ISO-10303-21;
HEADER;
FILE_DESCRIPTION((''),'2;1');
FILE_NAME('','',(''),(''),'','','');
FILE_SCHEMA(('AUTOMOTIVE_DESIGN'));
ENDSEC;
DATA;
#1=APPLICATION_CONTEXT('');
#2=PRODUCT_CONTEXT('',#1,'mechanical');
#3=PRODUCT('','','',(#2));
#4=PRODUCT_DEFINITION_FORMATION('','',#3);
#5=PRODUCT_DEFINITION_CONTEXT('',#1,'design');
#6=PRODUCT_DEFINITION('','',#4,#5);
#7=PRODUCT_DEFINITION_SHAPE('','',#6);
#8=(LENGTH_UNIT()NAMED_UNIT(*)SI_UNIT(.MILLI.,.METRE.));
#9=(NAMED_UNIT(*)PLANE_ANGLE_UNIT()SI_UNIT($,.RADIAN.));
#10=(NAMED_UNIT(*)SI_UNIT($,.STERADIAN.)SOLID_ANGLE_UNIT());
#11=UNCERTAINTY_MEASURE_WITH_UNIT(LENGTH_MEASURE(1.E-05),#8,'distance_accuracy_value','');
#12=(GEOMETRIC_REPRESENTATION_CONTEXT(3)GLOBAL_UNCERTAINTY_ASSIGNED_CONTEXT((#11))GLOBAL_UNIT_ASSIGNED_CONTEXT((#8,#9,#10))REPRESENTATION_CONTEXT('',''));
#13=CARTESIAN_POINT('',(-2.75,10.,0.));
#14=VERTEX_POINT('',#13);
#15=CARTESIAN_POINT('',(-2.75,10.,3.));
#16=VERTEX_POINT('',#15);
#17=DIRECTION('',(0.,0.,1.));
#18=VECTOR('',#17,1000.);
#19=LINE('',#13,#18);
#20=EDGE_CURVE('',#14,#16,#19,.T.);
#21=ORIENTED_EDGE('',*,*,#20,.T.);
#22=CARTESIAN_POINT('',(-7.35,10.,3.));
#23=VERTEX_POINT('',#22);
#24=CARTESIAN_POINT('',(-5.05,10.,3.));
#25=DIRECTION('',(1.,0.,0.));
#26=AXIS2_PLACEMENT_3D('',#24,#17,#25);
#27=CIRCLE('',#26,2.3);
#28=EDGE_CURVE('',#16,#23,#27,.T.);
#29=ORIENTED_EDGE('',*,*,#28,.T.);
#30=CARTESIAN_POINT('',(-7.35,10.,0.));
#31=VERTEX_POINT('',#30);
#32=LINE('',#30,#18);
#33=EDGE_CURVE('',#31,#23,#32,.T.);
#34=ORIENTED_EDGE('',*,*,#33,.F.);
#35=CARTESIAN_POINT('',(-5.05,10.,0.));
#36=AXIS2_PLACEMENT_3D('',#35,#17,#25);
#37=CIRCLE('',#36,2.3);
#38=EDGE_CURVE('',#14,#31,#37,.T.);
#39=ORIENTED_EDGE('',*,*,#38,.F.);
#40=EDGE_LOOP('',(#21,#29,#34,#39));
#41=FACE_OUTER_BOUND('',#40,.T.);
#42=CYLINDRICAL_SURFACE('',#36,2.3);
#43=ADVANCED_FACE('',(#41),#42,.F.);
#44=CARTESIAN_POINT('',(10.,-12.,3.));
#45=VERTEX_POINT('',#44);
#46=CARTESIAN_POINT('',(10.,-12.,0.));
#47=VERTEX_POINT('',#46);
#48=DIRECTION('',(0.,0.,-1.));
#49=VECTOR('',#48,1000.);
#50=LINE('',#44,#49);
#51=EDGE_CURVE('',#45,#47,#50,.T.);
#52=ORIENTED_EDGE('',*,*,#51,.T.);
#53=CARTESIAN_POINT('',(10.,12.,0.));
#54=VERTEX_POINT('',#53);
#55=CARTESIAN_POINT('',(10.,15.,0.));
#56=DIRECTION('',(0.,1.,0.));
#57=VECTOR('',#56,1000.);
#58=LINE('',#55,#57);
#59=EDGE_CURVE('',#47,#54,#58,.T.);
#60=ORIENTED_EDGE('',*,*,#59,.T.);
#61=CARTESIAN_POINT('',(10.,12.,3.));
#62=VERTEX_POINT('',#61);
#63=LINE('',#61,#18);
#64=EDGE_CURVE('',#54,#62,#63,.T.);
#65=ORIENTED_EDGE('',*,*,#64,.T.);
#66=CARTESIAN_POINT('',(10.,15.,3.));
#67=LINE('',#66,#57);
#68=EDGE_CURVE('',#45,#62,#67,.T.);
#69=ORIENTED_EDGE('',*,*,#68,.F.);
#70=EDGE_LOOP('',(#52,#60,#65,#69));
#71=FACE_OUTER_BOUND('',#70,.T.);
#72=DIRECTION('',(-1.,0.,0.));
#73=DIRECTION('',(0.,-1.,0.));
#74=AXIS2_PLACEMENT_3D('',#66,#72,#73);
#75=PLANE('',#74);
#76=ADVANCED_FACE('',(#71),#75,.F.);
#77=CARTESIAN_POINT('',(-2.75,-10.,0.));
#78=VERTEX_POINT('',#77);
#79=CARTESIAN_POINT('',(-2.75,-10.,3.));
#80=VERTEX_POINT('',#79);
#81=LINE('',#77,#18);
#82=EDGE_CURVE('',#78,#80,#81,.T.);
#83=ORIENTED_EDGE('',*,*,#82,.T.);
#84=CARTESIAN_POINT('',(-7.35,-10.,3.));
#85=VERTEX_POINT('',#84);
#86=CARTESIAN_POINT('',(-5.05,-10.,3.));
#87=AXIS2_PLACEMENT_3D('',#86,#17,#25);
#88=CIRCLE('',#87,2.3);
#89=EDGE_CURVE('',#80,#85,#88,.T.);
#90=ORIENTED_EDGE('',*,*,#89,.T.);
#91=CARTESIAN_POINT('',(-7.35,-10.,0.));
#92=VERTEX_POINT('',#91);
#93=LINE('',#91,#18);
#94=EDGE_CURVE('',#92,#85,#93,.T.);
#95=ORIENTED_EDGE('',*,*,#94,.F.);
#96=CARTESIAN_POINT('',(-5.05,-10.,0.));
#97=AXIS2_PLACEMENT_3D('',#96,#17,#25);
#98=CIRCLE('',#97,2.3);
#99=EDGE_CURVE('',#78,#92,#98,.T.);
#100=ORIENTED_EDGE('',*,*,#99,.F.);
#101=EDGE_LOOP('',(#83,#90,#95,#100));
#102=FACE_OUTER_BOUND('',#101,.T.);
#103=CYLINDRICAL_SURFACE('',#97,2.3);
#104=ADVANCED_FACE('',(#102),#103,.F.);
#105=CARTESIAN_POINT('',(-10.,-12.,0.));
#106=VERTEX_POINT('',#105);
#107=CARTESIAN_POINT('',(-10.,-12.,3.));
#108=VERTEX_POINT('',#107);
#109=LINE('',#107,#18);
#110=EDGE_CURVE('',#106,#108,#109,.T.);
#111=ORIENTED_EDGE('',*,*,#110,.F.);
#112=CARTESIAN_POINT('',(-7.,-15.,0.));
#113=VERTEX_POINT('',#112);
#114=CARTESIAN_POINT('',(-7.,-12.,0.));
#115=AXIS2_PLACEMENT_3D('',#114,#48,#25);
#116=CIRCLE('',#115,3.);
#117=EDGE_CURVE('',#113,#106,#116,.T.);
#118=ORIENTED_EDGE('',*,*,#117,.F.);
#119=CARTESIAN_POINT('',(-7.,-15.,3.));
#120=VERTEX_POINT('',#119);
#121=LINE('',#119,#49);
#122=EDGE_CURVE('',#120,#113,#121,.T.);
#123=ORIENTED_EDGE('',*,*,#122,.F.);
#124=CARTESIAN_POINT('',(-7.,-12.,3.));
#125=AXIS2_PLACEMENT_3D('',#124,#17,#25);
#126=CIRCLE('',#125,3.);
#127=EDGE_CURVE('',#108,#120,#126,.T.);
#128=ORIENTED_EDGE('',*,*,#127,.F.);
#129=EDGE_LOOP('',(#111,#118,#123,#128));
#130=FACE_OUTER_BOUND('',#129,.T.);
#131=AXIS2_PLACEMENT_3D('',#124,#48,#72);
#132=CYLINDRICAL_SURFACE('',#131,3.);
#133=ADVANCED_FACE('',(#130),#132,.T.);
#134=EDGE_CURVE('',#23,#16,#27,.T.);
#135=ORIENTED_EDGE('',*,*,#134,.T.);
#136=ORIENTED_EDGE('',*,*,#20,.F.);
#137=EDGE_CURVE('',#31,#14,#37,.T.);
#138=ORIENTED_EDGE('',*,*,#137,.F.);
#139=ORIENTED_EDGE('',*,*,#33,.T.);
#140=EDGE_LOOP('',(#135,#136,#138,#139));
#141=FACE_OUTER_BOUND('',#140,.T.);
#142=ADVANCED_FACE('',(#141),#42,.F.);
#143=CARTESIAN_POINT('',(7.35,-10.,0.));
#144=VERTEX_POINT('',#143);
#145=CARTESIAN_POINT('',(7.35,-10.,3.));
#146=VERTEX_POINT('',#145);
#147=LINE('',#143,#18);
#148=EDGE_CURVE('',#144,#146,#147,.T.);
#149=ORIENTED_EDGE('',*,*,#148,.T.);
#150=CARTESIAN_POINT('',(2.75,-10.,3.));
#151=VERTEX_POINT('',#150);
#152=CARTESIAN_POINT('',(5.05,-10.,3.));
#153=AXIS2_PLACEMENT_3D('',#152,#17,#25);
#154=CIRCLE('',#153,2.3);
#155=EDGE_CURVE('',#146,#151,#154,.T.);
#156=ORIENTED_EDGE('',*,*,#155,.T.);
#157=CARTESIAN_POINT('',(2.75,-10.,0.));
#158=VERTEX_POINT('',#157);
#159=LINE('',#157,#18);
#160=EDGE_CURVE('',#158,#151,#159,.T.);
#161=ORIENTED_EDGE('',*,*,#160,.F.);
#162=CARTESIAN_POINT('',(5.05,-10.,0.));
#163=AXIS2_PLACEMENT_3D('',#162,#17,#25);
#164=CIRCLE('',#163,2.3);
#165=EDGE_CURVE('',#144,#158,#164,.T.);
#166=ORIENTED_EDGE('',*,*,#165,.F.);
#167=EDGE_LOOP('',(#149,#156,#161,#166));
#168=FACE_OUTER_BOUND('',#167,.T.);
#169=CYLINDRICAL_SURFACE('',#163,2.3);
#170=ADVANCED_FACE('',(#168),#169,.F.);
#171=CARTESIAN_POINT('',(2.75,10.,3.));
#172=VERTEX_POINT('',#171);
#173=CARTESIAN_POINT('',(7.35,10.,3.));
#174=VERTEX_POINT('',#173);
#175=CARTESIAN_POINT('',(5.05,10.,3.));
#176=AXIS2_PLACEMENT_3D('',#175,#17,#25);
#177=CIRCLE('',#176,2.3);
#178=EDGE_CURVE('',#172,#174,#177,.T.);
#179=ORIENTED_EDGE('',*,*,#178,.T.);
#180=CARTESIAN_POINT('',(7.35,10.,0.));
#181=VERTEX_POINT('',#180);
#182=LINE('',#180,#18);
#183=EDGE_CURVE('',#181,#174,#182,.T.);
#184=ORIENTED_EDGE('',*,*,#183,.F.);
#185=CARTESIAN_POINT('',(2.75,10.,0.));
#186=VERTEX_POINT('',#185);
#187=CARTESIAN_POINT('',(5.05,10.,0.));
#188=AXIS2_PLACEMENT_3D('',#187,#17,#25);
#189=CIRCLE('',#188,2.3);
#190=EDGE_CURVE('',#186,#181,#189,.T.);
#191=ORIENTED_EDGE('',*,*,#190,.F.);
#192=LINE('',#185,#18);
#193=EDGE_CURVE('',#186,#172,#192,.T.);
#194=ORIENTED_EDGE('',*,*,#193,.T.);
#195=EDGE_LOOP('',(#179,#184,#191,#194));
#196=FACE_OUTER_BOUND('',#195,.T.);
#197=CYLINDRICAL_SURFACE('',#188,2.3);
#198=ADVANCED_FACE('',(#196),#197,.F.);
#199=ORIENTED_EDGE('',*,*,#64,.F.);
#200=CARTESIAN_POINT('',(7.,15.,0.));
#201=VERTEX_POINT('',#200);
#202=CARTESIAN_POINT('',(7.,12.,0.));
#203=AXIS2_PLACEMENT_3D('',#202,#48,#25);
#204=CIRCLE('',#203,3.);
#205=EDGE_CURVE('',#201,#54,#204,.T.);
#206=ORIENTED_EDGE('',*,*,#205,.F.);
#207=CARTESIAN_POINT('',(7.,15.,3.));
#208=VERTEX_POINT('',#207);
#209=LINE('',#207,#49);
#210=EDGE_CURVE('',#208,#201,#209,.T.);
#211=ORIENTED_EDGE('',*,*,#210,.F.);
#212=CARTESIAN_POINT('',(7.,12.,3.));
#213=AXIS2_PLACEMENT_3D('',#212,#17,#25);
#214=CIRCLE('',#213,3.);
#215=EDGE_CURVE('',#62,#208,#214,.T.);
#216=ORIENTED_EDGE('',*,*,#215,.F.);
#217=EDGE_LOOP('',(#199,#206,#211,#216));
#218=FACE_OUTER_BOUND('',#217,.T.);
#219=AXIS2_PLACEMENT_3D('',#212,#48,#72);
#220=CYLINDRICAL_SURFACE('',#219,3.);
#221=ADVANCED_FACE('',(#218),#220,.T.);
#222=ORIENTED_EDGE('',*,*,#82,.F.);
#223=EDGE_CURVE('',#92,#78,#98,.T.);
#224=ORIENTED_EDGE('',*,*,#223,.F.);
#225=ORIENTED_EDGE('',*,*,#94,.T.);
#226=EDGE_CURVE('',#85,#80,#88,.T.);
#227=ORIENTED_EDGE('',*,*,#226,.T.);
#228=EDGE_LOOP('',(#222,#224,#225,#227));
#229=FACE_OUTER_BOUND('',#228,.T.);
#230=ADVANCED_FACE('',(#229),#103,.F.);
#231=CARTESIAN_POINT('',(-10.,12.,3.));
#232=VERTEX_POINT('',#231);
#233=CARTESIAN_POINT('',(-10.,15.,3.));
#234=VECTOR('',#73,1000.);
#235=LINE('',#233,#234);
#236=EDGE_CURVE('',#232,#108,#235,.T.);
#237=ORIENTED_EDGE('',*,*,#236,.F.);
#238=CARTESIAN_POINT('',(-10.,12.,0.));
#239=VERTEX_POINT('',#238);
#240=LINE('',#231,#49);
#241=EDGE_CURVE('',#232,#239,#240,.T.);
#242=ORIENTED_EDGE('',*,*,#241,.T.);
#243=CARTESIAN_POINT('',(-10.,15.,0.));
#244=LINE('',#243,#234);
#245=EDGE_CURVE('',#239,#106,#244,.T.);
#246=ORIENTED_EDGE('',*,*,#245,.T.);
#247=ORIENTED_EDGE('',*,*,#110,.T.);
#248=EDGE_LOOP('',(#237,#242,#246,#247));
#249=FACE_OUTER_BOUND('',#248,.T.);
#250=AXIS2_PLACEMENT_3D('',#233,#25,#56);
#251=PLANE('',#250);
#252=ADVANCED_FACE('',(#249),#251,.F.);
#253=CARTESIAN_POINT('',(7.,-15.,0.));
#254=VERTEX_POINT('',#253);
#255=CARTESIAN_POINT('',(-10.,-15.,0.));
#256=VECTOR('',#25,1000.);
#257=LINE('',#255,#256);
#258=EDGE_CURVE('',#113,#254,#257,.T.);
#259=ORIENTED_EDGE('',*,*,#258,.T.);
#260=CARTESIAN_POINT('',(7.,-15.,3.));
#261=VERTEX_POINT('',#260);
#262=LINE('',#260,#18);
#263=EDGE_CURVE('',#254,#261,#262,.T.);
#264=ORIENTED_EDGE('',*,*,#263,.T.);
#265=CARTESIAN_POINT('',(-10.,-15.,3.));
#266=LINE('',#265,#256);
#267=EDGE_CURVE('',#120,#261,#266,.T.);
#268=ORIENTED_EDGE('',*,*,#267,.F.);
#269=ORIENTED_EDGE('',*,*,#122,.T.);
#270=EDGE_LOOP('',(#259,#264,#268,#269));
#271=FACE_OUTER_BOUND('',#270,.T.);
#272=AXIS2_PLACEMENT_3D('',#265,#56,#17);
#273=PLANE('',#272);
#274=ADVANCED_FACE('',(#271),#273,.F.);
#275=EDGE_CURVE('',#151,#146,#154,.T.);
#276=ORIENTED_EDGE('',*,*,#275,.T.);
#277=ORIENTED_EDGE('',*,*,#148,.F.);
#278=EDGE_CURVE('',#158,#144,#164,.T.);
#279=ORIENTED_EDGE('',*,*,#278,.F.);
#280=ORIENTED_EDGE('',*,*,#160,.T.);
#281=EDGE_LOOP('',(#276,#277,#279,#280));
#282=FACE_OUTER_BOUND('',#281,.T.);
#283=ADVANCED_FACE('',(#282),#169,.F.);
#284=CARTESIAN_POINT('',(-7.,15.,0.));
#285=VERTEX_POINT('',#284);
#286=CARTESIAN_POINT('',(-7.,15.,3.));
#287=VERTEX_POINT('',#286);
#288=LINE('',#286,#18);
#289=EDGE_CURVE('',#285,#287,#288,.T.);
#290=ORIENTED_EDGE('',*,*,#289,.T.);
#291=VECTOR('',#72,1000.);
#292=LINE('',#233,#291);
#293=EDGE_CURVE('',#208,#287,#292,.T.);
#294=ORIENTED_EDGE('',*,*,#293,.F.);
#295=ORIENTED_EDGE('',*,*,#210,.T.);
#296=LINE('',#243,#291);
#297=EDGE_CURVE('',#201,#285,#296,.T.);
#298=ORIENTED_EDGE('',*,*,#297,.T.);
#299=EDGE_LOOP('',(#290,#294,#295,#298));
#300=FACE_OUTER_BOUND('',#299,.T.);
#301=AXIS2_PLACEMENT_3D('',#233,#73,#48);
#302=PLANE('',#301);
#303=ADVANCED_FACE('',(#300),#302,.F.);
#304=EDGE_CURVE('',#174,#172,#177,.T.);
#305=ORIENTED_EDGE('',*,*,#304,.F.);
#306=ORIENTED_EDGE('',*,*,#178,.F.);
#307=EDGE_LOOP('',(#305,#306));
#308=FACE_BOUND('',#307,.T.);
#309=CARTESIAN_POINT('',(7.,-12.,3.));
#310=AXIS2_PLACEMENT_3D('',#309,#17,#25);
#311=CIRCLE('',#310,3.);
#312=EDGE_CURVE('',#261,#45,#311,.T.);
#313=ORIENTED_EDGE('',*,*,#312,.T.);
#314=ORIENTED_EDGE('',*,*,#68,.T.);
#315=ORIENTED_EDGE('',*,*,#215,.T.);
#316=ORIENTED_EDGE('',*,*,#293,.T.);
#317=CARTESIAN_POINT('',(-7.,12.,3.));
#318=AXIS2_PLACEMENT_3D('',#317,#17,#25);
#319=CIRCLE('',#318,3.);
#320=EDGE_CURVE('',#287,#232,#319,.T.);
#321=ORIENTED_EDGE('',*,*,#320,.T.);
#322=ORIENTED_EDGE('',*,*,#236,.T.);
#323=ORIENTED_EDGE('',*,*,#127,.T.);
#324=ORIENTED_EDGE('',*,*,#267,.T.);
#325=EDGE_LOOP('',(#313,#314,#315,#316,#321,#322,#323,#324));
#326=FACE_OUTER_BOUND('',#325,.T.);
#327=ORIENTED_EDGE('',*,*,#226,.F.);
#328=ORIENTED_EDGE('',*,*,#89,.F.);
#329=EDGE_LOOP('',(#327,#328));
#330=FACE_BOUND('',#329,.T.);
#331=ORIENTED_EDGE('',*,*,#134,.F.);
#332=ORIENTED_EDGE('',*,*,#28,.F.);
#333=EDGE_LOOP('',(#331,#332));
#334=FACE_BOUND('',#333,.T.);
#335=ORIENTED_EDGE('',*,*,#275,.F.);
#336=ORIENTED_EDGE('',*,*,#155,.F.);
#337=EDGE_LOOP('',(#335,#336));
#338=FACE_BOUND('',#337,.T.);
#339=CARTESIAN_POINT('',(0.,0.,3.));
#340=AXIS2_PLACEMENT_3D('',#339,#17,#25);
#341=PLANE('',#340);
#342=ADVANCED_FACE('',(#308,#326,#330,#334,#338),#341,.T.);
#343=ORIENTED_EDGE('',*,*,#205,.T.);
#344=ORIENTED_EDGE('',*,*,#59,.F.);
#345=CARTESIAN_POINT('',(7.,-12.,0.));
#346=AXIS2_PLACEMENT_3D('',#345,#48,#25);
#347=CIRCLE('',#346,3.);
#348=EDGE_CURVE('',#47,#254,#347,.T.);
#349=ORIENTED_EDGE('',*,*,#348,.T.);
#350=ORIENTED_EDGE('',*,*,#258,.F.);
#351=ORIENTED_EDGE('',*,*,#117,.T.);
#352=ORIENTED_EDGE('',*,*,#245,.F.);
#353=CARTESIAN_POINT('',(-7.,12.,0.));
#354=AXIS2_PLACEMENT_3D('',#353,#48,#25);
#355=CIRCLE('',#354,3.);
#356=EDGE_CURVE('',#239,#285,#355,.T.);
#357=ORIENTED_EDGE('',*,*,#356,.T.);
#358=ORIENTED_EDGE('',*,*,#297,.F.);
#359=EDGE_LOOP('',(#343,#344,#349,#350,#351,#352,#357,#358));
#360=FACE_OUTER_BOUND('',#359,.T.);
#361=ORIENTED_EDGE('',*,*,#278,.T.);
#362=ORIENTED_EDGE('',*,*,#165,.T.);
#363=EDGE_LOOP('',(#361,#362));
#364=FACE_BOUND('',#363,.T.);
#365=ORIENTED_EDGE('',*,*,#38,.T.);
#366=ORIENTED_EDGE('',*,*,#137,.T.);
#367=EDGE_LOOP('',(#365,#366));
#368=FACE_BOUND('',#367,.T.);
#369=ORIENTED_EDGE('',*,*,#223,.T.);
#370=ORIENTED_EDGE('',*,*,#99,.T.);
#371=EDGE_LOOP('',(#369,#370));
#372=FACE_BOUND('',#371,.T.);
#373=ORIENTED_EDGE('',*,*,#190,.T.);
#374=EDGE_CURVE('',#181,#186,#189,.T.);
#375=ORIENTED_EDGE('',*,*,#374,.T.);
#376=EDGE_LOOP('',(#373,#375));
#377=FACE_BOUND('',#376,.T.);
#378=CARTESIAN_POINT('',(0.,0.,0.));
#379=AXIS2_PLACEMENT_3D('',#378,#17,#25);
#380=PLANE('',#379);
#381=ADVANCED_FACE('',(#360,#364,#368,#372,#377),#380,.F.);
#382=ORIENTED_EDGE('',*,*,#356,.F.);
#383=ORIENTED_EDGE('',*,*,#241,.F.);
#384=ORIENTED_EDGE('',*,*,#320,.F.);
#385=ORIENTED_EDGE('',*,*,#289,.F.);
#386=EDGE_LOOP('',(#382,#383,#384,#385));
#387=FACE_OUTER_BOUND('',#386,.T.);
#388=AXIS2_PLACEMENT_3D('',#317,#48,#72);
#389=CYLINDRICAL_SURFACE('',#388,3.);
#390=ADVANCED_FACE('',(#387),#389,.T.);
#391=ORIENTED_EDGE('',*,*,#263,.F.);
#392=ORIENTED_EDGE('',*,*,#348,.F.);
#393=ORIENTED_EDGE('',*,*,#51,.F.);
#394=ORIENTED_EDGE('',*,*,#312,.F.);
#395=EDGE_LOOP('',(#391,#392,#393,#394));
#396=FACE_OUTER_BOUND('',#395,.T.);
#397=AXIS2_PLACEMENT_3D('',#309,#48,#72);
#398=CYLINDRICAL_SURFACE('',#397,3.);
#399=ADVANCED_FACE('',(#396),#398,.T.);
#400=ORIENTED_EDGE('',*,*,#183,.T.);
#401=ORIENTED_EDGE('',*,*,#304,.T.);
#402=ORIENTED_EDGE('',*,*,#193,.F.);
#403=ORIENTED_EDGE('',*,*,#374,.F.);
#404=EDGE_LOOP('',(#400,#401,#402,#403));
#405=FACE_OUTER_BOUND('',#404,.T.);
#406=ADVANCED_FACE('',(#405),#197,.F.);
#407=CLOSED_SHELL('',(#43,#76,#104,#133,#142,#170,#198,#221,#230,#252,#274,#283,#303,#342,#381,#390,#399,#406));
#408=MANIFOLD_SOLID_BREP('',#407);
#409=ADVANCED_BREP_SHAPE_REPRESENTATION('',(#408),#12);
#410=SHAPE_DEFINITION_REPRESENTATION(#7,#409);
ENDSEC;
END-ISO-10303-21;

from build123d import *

# Parameters (mm, degrees)
SKETCH1_W           = 20
SKETCH1_H           = 30
BOSS_EXTRUDE1_DEPTH = 3
SKETCH2_R           = 2.3
CUT_EXTRUDE1_DEPTH  = 3
FILLET1_R           = 3


with BuildPart() as part:
    # Sketch1 → Boss-Extrude1 (new body)
    with BuildSketch(Plane.XY):
        Rectangle(SKETCH1_W, SKETCH1_H)
    extrude(amount=BOSS_EXTRUDE1_DEPTH)

    # Sketch2 → Cut-Extrude1 (cut)
    with BuildSketch(Plane.XY.offset(3)):
        with Locations((-5.05, 10)):
            Circle(SKETCH2_R)
        with Locations((5.05, 10)):
            Circle(SKETCH2_R)
        with Locations((-5.05, -10)):
            Circle(SKETCH2_R)
        with Locations((5.05, -10)):
            Circle(SKETCH2_R)
    extrude(amount=-CUT_EXTRUDE1_DEPTH, mode=Mode.SUBTRACT)

    # Fillet1
    fillet1_edges = [part.edges().sort_by_distance(p)[0] for p in [
        (10, -15, 1.5),
        (-10, -15, 1.5),
        (-10, 15, 1.5),
        (10, 15, 1.5),
    ]]
    fillet(fillet1_edges, radius=FILLET1_R)


solid = part.part
